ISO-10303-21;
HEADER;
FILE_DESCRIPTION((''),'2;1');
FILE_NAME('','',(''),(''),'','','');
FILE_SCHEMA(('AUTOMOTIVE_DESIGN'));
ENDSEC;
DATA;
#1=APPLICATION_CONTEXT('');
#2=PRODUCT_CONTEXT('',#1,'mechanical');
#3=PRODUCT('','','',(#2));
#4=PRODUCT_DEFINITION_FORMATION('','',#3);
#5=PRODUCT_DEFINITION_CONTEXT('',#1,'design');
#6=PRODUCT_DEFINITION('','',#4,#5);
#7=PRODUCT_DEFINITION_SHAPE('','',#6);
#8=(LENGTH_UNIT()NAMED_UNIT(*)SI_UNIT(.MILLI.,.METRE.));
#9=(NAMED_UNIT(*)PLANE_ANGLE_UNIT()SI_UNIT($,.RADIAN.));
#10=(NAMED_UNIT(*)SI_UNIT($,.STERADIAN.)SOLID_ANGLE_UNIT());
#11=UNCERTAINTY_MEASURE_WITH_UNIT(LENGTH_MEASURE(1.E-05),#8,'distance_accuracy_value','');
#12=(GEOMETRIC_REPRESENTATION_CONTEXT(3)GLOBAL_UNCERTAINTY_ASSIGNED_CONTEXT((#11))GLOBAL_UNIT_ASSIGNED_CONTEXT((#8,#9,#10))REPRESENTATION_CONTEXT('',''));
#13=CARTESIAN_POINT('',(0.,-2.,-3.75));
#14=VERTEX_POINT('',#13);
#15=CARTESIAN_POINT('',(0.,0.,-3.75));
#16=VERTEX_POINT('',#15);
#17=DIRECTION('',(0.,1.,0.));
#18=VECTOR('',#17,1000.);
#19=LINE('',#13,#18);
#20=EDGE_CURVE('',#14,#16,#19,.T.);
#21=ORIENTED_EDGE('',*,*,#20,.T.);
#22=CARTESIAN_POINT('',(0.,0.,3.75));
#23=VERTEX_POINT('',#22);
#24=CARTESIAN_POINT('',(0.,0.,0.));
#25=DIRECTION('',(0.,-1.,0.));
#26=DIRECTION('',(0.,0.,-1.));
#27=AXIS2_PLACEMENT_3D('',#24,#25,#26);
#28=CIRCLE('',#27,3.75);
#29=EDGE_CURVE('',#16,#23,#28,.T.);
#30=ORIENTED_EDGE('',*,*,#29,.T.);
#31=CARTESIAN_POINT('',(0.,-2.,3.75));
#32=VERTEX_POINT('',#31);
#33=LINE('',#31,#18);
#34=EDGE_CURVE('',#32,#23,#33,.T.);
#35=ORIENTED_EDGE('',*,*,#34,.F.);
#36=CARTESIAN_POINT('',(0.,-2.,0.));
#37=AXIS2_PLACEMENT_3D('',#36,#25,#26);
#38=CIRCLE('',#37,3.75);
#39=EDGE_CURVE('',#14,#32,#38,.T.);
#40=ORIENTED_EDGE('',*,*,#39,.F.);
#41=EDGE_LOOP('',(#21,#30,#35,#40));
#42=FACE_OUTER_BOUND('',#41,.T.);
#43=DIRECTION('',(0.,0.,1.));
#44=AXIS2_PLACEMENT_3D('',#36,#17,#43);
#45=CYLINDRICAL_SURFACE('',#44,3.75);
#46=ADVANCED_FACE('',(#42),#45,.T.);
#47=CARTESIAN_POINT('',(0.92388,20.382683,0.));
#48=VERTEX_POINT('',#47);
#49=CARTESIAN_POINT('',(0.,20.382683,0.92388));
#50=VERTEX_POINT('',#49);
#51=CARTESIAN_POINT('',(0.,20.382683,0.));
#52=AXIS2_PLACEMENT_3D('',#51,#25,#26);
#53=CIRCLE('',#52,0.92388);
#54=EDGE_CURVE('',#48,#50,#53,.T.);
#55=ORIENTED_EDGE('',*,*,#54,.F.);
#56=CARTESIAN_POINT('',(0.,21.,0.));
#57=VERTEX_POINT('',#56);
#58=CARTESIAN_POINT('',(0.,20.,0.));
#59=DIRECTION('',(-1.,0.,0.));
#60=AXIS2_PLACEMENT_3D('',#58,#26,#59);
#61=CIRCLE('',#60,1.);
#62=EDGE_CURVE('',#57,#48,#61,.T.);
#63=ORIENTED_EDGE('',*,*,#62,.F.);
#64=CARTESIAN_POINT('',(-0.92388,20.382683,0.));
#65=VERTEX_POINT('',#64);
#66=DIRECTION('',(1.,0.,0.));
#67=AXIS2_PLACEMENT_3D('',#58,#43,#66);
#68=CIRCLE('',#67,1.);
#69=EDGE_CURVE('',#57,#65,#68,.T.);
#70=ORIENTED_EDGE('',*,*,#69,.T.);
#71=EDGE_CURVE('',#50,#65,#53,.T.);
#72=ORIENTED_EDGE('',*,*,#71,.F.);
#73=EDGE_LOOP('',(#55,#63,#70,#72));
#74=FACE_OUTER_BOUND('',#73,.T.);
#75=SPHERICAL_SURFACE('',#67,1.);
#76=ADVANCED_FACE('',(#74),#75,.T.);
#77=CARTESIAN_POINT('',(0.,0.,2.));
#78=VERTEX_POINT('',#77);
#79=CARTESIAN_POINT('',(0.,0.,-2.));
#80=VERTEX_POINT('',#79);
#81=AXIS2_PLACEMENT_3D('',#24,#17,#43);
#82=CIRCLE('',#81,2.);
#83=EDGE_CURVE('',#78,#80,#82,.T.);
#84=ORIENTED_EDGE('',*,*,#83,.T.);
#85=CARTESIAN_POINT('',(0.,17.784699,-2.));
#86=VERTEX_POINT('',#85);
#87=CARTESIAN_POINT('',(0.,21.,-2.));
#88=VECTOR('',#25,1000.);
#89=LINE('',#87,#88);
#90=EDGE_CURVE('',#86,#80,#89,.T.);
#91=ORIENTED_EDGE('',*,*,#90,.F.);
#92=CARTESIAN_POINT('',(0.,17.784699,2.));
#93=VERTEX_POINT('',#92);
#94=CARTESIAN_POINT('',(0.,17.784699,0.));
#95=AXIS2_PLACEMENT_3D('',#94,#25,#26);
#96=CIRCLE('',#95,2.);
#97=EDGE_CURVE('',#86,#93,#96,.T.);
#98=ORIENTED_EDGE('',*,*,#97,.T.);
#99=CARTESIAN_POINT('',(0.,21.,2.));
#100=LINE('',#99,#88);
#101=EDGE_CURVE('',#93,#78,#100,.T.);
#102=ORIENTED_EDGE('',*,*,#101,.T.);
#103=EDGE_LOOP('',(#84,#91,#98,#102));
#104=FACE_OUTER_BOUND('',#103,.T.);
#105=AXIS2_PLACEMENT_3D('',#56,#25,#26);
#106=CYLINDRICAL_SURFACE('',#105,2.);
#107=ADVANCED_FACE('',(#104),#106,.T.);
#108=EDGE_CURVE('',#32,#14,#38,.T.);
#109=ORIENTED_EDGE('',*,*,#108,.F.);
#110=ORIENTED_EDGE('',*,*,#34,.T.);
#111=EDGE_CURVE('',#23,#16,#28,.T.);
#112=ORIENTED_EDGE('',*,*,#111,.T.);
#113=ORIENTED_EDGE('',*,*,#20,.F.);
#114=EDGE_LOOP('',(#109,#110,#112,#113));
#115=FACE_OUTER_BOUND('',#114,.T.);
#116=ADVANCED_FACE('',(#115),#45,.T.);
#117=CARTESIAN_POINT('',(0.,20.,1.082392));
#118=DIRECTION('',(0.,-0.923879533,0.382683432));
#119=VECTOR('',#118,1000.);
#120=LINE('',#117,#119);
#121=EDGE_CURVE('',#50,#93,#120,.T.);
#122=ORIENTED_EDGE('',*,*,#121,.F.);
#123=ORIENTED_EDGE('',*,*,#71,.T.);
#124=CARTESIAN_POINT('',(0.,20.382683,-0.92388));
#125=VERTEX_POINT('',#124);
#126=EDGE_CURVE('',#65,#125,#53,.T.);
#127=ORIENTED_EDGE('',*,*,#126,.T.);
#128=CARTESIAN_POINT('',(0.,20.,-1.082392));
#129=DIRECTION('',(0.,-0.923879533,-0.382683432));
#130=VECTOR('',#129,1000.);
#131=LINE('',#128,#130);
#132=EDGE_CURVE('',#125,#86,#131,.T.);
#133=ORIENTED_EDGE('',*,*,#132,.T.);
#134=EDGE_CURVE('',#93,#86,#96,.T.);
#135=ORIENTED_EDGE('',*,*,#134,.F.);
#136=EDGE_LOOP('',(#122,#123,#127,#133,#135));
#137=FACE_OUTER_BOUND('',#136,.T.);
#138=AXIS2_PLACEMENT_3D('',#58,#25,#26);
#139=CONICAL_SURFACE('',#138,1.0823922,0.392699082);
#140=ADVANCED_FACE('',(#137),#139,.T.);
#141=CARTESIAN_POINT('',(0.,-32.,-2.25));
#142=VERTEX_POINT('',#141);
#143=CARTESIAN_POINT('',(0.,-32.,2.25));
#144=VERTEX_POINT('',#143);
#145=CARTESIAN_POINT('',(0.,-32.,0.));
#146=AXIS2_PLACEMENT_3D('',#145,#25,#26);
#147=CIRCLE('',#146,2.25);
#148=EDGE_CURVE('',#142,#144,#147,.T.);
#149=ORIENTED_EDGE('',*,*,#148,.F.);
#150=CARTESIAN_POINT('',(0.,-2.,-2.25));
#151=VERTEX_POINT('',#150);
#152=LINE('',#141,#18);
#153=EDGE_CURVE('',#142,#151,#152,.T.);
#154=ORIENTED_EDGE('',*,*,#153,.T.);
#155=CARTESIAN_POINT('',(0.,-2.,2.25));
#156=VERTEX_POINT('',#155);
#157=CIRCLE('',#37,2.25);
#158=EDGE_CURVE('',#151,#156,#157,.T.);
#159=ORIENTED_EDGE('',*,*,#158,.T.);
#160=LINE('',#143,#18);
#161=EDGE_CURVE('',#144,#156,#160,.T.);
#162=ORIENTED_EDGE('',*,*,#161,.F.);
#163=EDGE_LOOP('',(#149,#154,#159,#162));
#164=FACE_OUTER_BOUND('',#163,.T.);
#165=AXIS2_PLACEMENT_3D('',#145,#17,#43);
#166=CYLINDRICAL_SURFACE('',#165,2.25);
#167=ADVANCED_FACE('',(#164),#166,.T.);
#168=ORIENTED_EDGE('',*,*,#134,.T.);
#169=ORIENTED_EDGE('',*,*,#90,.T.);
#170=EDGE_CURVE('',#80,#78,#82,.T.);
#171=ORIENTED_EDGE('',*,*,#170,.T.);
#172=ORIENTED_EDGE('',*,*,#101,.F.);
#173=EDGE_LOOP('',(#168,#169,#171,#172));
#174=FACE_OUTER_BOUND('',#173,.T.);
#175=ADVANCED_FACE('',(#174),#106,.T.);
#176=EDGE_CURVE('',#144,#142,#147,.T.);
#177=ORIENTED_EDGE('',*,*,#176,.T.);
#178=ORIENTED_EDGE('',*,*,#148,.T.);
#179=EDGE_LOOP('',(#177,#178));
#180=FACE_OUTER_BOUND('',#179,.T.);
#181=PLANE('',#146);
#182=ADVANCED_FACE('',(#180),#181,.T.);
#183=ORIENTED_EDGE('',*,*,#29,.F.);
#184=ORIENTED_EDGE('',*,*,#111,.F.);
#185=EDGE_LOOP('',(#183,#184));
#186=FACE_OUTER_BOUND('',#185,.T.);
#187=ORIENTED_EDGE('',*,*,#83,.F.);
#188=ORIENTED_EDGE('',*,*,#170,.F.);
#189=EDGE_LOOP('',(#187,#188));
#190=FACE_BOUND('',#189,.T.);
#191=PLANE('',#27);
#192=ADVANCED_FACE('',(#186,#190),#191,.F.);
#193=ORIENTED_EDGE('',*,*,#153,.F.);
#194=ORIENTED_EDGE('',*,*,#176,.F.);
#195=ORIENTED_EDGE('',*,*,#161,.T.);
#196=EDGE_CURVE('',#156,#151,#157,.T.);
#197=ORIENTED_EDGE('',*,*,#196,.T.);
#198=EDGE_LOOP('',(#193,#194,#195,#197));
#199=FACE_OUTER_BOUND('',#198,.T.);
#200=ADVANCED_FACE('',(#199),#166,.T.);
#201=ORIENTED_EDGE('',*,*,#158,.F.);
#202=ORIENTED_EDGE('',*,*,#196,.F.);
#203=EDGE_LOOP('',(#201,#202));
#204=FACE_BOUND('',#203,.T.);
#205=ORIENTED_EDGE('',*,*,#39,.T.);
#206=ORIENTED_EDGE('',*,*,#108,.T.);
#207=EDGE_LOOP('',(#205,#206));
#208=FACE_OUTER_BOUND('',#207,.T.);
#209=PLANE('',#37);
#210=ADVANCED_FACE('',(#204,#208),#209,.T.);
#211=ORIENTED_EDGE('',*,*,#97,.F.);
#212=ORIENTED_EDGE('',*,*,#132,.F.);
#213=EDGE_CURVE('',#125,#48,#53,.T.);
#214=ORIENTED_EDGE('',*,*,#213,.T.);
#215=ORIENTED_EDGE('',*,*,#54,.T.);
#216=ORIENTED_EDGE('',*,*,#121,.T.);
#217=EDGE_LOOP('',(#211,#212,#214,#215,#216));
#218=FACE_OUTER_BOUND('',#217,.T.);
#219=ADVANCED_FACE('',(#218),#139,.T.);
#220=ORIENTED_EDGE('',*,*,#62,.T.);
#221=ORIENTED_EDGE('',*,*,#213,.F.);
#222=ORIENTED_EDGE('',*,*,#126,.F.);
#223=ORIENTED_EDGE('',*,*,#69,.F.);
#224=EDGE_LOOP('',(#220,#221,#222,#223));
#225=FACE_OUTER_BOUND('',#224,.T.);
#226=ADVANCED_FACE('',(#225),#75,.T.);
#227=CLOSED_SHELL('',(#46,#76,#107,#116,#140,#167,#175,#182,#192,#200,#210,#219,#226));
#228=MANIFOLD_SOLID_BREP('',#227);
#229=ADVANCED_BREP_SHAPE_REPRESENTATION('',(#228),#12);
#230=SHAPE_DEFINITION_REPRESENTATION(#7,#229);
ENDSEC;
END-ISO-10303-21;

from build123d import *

# Parameters (mm, degrees)
SKETCH1_R           = 2.5
BOSS_EXTRUDE1_DEPTH = 20
SKETCH2_R           = 3.75
BOSS_EXTRUDE2_DEPTH = 2
SKETCH3_R           = 2.25
BOSS_EXTRUDE3_DEPTH = 30
SKETCH7_R           = 4
SKETCH7_R_2         = 2
CUT_EXTRUDE1_DEPTH  = 33.436476381


with BuildPart() as part:
    # Sketch1 → Boss-Extrude1 (new body)
    with BuildSketch(Plane(origin=(0, 0, 0), x_dir=(1, 0, 0), z_dir=(0, 1, 0))):
        with Locations(Location((0, 0, 0), (0, 0, 270))):
            Circle(SKETCH1_R)
    extrude(amount=BOSS_EXTRUDE1_DEPTH)

    # Sketch2 → Boss-Extrude2 (add)
    with BuildSketch(Plane.XZ):
        with Locations(Location((0, 0, 0), (0, 0, 270))):
            Circle(SKETCH2_R)
    extrude(amount=BOSS_EXTRUDE2_DEPTH)

    # Sketch3 → Boss-Extrude3 (add)
    with BuildSketch(Plane.XZ.offset(2)):
        with Locations(Location((0, 0, 0), (0, 0, 270))):
            Circle(SKETCH3_R)
    extrude(amount=BOSS_EXTRUDE3_DEPTH)

    # Sketch4 → Revolve1 (revolve)
    with BuildSketch(Plane.XY, mode=Mode.PRIVATE) as revolve1_sk:
        with BuildLine():
            Line((1, 20), (0, 20))
            Line((0, 20), (0, 21))
            ThreePointArc((0, 21), (0.707106781, 20.707106781), (1, 20))
        make_face()
    revolve(revolve1_sk.sketch.rotate(Axis((0, 20, 0), (0, 1, 0)), 90), axis=Axis((0, 20, 0), (0, 1, 0)))

    # Sketch5 → Cut-Revolve1 (revolve, cut)
    with BuildSketch(Plane(origin=(0, 0, 0), x_dir=(0, 0, -1), z_dir=(1, 0, 0)), mode=Mode.PRIVATE) as cut_revolve1_sk:
        Polygon((1.0823922, 20), (2.5, 16.577592024), (2.5, 20), align=None)
    revolve(cut_revolve1_sk.sketch.rotate(Axis((0, 15, 0), (0, -1, 0)), 90), axis=Axis((0, 15, 0), (0, -1, 0)), mode=Mode.SUBTRACT)

    # Sketch6 → Revolve2 (revolve)
    with BuildSketch(Plane(origin=(0, 0, 0), x_dir=(0, 0, -1), z_dir=(1, 0, 0))):
        with BuildLine():
            Line((1.0823922, 20), (0.923879533, 20.382683432))
            ThreePointArc((0.923879533, 20.382683432), (0.98078528, 20.195090322), (1, 20))
            Line((1, 20), (1.0823922, 20))
        make_face()
    revolve(axis=Axis((0, 16, 0), (0, 1, 0)))

    # Sketch7 → Cut-Extrude1 (cut, through all)
    with BuildSketch(Plane(origin=(0, 0, 0), x_dir=(1, 0, 0), z_dir=(0, 1, 0))):
        Circle(SKETCH7_R)
        with Locations(Location((0, 0, 0), (0, 0, 90))):
            Circle(SKETCH7_R_2, mode=Mode.SUBTRACT)
    extrude(amount=CUT_EXTRUDE1_DEPTH, mode=Mode.SUBTRACT)


solid = part.part
